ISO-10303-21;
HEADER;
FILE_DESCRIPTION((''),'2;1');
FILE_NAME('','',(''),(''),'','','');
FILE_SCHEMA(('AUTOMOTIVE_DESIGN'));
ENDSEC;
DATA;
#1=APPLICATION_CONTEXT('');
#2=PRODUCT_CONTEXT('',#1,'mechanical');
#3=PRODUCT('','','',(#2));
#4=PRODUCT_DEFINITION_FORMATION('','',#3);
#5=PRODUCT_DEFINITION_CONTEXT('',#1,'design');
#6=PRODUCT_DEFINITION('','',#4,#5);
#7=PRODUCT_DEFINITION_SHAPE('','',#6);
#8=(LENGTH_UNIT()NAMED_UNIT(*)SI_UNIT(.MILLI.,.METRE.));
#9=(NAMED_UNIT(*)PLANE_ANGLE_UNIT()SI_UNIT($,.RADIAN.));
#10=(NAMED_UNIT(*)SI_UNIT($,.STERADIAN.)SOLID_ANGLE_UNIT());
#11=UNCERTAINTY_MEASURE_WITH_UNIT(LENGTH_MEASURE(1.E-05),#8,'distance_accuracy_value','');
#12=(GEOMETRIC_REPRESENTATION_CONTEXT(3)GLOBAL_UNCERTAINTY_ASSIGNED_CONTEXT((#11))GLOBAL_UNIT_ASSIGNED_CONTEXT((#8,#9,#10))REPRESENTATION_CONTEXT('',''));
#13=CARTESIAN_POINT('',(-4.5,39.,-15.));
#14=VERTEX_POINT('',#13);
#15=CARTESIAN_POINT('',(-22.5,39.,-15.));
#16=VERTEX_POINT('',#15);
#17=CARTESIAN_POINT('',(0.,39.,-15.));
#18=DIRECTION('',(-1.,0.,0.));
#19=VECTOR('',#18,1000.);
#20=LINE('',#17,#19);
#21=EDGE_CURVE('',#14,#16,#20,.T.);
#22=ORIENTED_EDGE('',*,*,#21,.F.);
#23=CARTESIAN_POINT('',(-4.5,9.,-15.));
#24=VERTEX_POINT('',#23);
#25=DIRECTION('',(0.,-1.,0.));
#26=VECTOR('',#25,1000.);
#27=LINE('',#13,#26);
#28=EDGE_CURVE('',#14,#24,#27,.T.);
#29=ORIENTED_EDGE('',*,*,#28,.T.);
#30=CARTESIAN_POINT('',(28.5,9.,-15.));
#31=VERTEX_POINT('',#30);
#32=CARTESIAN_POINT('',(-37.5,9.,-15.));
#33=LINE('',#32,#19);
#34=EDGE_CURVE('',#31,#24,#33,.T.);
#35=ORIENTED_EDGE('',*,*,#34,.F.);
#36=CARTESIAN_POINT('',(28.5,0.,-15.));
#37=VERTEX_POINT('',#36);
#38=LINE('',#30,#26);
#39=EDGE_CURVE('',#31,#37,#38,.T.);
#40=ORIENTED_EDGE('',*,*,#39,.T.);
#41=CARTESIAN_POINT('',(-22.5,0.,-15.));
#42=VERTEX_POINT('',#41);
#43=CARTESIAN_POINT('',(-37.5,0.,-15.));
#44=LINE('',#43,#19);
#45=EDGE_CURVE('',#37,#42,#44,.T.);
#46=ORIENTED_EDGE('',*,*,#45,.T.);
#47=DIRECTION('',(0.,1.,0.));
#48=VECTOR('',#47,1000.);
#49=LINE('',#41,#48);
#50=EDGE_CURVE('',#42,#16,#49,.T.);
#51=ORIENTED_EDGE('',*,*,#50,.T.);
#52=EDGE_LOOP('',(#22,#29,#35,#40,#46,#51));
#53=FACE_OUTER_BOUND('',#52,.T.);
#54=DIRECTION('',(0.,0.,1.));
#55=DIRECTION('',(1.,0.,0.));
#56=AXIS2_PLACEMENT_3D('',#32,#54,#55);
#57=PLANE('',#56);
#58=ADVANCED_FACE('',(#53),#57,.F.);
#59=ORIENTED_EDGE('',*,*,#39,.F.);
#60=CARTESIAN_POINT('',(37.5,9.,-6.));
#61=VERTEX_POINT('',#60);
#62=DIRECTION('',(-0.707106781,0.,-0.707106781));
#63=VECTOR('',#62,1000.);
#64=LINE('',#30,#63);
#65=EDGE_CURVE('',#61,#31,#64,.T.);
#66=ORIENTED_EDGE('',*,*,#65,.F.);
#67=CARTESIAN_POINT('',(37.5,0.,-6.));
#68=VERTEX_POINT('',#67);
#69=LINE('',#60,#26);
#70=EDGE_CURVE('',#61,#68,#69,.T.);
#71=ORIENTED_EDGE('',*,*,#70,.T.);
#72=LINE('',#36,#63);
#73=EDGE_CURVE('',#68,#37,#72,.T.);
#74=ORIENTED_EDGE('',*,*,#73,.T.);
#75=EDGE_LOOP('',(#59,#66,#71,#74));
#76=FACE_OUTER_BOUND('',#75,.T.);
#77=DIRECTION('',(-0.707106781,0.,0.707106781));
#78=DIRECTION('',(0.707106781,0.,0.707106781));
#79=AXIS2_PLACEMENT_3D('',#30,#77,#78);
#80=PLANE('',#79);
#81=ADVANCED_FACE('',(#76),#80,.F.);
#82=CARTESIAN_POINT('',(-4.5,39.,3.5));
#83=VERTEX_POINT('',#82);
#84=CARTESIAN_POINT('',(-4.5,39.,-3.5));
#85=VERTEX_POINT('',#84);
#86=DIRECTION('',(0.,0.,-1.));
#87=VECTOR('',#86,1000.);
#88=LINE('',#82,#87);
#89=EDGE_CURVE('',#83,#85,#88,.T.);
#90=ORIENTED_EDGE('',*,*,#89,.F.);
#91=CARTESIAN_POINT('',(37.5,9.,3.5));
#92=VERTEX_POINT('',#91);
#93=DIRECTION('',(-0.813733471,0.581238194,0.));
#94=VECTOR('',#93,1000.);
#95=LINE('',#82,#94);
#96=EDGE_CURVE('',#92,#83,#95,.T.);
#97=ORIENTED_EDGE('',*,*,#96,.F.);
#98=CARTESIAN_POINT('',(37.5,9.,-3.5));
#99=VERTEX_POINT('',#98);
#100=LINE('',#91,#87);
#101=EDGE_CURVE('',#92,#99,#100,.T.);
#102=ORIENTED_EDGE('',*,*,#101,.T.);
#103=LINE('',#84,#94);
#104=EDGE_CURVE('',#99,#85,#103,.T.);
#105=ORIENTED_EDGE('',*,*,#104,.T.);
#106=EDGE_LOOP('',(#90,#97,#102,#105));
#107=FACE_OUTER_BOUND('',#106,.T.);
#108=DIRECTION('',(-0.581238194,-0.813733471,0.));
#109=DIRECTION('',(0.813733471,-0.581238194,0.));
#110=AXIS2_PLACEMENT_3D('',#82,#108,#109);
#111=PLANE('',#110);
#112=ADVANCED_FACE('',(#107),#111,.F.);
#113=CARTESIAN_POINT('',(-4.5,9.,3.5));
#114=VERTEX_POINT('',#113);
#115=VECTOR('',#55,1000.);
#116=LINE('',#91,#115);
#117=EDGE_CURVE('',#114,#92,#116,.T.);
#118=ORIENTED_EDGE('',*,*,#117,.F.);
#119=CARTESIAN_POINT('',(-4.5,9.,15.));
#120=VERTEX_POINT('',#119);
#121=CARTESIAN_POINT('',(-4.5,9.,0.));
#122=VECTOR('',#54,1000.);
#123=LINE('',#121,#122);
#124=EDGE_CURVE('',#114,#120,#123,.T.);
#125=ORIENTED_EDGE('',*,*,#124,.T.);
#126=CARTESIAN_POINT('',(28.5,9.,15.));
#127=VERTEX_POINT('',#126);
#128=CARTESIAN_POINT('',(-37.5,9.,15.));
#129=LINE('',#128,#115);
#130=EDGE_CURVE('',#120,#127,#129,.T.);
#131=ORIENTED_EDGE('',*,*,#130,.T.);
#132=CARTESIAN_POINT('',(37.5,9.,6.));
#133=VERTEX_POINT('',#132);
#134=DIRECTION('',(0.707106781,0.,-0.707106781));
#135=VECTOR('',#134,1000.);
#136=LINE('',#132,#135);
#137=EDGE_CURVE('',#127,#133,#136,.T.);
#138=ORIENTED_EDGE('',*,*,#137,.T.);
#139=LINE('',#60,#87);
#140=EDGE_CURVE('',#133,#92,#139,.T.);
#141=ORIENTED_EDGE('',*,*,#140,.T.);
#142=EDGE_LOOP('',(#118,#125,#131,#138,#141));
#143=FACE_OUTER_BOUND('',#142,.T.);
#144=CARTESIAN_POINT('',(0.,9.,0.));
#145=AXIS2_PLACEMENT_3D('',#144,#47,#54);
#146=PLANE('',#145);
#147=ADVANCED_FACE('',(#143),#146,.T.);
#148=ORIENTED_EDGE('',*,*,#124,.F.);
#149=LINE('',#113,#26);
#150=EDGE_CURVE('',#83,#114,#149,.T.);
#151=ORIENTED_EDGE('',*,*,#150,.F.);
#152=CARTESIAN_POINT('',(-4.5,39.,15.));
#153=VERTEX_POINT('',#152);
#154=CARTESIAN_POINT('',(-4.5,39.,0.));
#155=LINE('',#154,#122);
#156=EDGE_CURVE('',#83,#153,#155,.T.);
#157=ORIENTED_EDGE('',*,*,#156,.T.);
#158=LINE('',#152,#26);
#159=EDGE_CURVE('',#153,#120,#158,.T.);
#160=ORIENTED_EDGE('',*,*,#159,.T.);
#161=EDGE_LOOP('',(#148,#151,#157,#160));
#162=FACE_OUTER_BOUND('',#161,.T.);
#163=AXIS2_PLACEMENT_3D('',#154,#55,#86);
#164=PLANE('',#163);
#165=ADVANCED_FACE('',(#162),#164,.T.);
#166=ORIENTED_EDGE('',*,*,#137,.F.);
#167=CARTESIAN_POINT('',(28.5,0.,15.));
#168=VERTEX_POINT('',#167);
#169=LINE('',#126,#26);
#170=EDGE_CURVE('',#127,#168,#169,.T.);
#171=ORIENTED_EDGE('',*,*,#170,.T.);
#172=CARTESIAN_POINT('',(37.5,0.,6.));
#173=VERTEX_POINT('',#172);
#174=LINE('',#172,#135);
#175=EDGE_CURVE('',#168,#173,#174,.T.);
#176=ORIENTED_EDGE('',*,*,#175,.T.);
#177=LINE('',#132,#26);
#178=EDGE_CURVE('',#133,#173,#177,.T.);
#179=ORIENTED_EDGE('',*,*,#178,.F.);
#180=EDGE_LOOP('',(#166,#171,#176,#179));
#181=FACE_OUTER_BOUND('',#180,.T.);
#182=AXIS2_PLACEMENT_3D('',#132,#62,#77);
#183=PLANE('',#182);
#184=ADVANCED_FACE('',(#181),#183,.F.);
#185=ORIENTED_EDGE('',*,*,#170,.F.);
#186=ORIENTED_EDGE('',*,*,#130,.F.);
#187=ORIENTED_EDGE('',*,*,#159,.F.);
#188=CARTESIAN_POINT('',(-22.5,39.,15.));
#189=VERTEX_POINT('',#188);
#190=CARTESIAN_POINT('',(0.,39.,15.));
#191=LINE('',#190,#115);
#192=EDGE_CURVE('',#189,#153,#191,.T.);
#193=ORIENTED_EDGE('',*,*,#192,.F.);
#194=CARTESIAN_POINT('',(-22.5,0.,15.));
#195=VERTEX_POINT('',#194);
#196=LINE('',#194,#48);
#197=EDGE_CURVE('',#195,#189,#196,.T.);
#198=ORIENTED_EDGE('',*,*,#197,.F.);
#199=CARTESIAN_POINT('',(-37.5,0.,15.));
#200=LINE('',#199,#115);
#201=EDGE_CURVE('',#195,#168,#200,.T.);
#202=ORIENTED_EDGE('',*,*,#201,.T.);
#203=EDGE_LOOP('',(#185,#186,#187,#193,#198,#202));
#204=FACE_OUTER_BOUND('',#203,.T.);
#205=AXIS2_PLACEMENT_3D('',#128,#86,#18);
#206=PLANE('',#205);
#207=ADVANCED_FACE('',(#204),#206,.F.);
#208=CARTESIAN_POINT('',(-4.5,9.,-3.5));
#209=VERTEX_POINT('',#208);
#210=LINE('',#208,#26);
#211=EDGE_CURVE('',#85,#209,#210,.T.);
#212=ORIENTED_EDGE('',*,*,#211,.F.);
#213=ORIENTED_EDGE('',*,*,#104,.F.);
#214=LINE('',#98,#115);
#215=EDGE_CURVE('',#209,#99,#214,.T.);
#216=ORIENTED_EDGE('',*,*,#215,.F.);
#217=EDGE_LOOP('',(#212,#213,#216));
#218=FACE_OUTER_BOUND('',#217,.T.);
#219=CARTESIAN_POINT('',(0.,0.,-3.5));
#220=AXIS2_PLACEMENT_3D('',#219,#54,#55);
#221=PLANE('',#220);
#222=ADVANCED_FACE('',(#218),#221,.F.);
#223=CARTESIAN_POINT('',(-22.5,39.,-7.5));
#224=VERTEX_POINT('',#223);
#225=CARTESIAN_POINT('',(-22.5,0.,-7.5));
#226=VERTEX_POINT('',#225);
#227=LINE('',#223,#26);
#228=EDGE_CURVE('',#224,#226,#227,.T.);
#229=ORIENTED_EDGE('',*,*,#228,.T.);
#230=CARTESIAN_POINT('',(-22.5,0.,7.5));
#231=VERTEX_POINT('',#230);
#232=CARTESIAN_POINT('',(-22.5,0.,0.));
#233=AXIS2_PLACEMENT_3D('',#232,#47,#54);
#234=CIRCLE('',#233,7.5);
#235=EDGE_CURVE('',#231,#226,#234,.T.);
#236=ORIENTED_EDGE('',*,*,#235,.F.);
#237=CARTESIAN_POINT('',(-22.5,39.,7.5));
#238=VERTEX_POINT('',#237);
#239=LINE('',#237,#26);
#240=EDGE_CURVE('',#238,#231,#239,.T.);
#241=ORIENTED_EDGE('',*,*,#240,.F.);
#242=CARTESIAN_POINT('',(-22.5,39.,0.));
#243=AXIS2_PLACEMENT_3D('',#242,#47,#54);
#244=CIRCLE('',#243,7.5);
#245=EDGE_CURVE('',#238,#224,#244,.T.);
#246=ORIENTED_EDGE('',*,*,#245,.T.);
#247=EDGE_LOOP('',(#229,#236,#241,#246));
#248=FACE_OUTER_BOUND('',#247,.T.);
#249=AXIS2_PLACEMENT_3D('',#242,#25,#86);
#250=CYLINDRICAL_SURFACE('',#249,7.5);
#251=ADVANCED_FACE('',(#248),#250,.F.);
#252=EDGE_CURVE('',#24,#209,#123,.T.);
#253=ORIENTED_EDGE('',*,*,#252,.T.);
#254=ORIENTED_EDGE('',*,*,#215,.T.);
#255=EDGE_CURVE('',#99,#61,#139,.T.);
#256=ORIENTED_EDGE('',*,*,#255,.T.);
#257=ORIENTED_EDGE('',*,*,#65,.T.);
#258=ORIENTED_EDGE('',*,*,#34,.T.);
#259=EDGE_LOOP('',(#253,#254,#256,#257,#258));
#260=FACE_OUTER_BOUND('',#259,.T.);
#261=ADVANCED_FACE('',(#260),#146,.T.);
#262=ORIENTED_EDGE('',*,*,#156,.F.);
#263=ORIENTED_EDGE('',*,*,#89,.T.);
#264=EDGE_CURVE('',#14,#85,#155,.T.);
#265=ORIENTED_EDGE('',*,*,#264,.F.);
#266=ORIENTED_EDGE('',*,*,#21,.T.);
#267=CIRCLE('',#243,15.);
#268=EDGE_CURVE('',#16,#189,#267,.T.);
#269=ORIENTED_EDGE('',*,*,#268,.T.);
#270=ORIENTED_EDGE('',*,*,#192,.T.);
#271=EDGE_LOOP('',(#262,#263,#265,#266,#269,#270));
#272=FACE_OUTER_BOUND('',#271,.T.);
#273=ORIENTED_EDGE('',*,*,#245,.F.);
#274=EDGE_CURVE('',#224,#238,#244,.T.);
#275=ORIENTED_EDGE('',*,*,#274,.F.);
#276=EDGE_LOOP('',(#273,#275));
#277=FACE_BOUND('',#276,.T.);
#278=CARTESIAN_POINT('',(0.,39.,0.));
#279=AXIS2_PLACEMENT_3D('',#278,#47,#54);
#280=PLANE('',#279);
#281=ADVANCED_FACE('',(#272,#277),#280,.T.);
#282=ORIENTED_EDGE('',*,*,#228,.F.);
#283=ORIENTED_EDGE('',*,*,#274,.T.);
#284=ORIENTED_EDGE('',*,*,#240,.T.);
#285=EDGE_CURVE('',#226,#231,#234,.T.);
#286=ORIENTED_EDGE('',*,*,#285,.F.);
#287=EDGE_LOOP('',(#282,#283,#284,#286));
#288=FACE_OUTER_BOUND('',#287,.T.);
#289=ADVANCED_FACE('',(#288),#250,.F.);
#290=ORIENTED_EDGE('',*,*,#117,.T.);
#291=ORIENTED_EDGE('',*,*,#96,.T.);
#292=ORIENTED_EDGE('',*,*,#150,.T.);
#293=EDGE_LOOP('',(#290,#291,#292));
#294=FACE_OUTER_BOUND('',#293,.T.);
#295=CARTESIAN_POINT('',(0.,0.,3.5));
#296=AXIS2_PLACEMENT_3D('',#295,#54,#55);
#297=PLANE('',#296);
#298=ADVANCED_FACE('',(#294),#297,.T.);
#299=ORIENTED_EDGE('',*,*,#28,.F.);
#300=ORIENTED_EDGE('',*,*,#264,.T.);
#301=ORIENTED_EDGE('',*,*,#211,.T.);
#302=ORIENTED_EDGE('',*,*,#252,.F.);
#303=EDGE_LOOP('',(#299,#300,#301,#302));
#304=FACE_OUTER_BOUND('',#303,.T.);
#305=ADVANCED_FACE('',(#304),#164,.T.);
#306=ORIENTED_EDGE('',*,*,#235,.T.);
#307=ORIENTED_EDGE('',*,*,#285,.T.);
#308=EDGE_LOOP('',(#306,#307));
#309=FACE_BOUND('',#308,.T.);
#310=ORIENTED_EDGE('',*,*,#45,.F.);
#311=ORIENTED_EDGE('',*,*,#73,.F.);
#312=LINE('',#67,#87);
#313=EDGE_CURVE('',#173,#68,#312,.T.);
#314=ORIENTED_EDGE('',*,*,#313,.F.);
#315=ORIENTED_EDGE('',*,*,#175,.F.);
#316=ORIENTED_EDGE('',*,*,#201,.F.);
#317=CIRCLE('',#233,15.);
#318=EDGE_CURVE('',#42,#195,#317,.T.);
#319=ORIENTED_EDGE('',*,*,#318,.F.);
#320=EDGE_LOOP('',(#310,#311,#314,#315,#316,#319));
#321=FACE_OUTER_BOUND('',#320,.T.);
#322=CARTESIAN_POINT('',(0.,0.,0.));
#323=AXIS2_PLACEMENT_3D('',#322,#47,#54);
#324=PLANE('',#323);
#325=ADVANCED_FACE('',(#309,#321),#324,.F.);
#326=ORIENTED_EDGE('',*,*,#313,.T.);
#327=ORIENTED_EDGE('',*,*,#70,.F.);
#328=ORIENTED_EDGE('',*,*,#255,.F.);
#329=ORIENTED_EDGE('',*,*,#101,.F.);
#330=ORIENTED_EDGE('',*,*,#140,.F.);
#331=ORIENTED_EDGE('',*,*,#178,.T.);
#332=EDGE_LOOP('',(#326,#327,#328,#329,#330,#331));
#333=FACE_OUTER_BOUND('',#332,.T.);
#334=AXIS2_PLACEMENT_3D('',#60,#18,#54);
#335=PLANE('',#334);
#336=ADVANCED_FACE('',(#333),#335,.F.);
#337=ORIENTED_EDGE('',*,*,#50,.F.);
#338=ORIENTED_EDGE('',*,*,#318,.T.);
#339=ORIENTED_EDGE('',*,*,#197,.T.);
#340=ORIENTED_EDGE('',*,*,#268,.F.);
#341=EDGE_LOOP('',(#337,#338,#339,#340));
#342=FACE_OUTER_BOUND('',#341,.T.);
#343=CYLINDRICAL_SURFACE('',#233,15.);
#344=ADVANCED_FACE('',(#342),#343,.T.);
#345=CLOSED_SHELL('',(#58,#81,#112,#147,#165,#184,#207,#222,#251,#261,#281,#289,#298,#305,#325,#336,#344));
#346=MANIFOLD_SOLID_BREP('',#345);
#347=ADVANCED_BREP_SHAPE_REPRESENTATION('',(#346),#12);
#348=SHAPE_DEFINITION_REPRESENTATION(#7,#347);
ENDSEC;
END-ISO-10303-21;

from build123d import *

# Parameters (mm, degrees)
BASE_PLATE_DEPTH      = 9
BASE_END_CUT_DEPTH    = 9
UPRIGHT_START         = 30
UPRIGHT_BOSS_SKETCH_R = 7.5
UPRIGHT_BOSS_DEPTH    = 30
SUPPORT_RIB_DEPTH     = 3.5
BOSS_BORE_SKETCH_R    = 7.5
BOSS_BORE_DEPTH       = 57.144901817


with BuildPart() as part:
    # Base Plate Sketch → Base Plate (new body)
    with BuildSketch(Plane(origin=(0, 0, 0), x_dir=(1, 0, 0), z_dir=(0, 1, 0))):
        Polygon((28.5, 15), (37.5, 6), (37.5, -6), (28.5, -15), (-37.5, -15), (-37.5, 15), align=None)
    extrude(amount=BASE_PLATE_DEPTH)

    # Base End Cut Sketch → Base End Cut (cut)
    with BuildSketch(Plane(origin=(0, 9, 0), x_dir=(1, 0, 0), z_dir=(0, 1, 0))):
        with BuildLine():
            Line((-37.5, 1.12e-07), (-37.5, -15))
            Line((-37.5, -15), (-22.5, -15))
            ThreePointArc((-22.5, -15), (-33.106601757, -10.606601678), (-37.5, 1.12e-07))
        make_face()
        with BuildLine():
            Line((-37.5, 15), (-37.5, 1.12e-07))
            ThreePointArc((-37.5, 1.12e-07), (-33.106601678, 10.606601757), (-22.5, 15))
            Line((-22.5, 15), (-37.5, 15))
        make_face()
    extrude(amount=-BASE_END_CUT_DEPTH, mode=Mode.SUBTRACT)

    # Upright Boss Sketch → Upright Boss (add)
    with BuildSketch(Plane(origin=(0, 9, 0), x_dir=(1, 0, 0), z_dir=(0, 1, 0)).offset(UPRIGHT_START)):
        with BuildLine():
            Line((-4.5, 15), (-22.5, 15))
            ThreePointArc((-22.5, 15), (-37.5, 0), (-22.5, -15))
            Line((-22.5, -15), (-4.5, -15))
            Line((-4.5, -15), (-4.5, 15))
        make_face()
        with Locations(Location((-22.5, 0, 0), (0, 0, 270))):
            Circle(UPRIGHT_BOSS_SKETCH_R, mode=Mode.SUBTRACT)
    extrude(amount=-UPRIGHT_BOSS_DEPTH)

    # Support Rib Sketch → Support Rib (add, symmetric)
    with BuildSketch(Plane.XY):
        Polygon((-4.5, 39), (37.5, 9), (-4.5, 9), align=None)
    extrude(amount=SUPPORT_RIB_DEPTH, both=True)

    # Boss Bore Sketch → Boss Bore (cut, through all)
    with BuildSketch(Plane(origin=(0, 39, 0), x_dir=(1, 0, 0), z_dir=(0, 1, 0))):
        with Locations(Location((-22.5, 0, 0), (0, 0, 270))):
            Circle(BOSS_BORE_SKETCH_R)
    extrude(amount=-BOSS_BORE_DEPTH, mode=Mode.SUBTRACT)


solid = part.part
